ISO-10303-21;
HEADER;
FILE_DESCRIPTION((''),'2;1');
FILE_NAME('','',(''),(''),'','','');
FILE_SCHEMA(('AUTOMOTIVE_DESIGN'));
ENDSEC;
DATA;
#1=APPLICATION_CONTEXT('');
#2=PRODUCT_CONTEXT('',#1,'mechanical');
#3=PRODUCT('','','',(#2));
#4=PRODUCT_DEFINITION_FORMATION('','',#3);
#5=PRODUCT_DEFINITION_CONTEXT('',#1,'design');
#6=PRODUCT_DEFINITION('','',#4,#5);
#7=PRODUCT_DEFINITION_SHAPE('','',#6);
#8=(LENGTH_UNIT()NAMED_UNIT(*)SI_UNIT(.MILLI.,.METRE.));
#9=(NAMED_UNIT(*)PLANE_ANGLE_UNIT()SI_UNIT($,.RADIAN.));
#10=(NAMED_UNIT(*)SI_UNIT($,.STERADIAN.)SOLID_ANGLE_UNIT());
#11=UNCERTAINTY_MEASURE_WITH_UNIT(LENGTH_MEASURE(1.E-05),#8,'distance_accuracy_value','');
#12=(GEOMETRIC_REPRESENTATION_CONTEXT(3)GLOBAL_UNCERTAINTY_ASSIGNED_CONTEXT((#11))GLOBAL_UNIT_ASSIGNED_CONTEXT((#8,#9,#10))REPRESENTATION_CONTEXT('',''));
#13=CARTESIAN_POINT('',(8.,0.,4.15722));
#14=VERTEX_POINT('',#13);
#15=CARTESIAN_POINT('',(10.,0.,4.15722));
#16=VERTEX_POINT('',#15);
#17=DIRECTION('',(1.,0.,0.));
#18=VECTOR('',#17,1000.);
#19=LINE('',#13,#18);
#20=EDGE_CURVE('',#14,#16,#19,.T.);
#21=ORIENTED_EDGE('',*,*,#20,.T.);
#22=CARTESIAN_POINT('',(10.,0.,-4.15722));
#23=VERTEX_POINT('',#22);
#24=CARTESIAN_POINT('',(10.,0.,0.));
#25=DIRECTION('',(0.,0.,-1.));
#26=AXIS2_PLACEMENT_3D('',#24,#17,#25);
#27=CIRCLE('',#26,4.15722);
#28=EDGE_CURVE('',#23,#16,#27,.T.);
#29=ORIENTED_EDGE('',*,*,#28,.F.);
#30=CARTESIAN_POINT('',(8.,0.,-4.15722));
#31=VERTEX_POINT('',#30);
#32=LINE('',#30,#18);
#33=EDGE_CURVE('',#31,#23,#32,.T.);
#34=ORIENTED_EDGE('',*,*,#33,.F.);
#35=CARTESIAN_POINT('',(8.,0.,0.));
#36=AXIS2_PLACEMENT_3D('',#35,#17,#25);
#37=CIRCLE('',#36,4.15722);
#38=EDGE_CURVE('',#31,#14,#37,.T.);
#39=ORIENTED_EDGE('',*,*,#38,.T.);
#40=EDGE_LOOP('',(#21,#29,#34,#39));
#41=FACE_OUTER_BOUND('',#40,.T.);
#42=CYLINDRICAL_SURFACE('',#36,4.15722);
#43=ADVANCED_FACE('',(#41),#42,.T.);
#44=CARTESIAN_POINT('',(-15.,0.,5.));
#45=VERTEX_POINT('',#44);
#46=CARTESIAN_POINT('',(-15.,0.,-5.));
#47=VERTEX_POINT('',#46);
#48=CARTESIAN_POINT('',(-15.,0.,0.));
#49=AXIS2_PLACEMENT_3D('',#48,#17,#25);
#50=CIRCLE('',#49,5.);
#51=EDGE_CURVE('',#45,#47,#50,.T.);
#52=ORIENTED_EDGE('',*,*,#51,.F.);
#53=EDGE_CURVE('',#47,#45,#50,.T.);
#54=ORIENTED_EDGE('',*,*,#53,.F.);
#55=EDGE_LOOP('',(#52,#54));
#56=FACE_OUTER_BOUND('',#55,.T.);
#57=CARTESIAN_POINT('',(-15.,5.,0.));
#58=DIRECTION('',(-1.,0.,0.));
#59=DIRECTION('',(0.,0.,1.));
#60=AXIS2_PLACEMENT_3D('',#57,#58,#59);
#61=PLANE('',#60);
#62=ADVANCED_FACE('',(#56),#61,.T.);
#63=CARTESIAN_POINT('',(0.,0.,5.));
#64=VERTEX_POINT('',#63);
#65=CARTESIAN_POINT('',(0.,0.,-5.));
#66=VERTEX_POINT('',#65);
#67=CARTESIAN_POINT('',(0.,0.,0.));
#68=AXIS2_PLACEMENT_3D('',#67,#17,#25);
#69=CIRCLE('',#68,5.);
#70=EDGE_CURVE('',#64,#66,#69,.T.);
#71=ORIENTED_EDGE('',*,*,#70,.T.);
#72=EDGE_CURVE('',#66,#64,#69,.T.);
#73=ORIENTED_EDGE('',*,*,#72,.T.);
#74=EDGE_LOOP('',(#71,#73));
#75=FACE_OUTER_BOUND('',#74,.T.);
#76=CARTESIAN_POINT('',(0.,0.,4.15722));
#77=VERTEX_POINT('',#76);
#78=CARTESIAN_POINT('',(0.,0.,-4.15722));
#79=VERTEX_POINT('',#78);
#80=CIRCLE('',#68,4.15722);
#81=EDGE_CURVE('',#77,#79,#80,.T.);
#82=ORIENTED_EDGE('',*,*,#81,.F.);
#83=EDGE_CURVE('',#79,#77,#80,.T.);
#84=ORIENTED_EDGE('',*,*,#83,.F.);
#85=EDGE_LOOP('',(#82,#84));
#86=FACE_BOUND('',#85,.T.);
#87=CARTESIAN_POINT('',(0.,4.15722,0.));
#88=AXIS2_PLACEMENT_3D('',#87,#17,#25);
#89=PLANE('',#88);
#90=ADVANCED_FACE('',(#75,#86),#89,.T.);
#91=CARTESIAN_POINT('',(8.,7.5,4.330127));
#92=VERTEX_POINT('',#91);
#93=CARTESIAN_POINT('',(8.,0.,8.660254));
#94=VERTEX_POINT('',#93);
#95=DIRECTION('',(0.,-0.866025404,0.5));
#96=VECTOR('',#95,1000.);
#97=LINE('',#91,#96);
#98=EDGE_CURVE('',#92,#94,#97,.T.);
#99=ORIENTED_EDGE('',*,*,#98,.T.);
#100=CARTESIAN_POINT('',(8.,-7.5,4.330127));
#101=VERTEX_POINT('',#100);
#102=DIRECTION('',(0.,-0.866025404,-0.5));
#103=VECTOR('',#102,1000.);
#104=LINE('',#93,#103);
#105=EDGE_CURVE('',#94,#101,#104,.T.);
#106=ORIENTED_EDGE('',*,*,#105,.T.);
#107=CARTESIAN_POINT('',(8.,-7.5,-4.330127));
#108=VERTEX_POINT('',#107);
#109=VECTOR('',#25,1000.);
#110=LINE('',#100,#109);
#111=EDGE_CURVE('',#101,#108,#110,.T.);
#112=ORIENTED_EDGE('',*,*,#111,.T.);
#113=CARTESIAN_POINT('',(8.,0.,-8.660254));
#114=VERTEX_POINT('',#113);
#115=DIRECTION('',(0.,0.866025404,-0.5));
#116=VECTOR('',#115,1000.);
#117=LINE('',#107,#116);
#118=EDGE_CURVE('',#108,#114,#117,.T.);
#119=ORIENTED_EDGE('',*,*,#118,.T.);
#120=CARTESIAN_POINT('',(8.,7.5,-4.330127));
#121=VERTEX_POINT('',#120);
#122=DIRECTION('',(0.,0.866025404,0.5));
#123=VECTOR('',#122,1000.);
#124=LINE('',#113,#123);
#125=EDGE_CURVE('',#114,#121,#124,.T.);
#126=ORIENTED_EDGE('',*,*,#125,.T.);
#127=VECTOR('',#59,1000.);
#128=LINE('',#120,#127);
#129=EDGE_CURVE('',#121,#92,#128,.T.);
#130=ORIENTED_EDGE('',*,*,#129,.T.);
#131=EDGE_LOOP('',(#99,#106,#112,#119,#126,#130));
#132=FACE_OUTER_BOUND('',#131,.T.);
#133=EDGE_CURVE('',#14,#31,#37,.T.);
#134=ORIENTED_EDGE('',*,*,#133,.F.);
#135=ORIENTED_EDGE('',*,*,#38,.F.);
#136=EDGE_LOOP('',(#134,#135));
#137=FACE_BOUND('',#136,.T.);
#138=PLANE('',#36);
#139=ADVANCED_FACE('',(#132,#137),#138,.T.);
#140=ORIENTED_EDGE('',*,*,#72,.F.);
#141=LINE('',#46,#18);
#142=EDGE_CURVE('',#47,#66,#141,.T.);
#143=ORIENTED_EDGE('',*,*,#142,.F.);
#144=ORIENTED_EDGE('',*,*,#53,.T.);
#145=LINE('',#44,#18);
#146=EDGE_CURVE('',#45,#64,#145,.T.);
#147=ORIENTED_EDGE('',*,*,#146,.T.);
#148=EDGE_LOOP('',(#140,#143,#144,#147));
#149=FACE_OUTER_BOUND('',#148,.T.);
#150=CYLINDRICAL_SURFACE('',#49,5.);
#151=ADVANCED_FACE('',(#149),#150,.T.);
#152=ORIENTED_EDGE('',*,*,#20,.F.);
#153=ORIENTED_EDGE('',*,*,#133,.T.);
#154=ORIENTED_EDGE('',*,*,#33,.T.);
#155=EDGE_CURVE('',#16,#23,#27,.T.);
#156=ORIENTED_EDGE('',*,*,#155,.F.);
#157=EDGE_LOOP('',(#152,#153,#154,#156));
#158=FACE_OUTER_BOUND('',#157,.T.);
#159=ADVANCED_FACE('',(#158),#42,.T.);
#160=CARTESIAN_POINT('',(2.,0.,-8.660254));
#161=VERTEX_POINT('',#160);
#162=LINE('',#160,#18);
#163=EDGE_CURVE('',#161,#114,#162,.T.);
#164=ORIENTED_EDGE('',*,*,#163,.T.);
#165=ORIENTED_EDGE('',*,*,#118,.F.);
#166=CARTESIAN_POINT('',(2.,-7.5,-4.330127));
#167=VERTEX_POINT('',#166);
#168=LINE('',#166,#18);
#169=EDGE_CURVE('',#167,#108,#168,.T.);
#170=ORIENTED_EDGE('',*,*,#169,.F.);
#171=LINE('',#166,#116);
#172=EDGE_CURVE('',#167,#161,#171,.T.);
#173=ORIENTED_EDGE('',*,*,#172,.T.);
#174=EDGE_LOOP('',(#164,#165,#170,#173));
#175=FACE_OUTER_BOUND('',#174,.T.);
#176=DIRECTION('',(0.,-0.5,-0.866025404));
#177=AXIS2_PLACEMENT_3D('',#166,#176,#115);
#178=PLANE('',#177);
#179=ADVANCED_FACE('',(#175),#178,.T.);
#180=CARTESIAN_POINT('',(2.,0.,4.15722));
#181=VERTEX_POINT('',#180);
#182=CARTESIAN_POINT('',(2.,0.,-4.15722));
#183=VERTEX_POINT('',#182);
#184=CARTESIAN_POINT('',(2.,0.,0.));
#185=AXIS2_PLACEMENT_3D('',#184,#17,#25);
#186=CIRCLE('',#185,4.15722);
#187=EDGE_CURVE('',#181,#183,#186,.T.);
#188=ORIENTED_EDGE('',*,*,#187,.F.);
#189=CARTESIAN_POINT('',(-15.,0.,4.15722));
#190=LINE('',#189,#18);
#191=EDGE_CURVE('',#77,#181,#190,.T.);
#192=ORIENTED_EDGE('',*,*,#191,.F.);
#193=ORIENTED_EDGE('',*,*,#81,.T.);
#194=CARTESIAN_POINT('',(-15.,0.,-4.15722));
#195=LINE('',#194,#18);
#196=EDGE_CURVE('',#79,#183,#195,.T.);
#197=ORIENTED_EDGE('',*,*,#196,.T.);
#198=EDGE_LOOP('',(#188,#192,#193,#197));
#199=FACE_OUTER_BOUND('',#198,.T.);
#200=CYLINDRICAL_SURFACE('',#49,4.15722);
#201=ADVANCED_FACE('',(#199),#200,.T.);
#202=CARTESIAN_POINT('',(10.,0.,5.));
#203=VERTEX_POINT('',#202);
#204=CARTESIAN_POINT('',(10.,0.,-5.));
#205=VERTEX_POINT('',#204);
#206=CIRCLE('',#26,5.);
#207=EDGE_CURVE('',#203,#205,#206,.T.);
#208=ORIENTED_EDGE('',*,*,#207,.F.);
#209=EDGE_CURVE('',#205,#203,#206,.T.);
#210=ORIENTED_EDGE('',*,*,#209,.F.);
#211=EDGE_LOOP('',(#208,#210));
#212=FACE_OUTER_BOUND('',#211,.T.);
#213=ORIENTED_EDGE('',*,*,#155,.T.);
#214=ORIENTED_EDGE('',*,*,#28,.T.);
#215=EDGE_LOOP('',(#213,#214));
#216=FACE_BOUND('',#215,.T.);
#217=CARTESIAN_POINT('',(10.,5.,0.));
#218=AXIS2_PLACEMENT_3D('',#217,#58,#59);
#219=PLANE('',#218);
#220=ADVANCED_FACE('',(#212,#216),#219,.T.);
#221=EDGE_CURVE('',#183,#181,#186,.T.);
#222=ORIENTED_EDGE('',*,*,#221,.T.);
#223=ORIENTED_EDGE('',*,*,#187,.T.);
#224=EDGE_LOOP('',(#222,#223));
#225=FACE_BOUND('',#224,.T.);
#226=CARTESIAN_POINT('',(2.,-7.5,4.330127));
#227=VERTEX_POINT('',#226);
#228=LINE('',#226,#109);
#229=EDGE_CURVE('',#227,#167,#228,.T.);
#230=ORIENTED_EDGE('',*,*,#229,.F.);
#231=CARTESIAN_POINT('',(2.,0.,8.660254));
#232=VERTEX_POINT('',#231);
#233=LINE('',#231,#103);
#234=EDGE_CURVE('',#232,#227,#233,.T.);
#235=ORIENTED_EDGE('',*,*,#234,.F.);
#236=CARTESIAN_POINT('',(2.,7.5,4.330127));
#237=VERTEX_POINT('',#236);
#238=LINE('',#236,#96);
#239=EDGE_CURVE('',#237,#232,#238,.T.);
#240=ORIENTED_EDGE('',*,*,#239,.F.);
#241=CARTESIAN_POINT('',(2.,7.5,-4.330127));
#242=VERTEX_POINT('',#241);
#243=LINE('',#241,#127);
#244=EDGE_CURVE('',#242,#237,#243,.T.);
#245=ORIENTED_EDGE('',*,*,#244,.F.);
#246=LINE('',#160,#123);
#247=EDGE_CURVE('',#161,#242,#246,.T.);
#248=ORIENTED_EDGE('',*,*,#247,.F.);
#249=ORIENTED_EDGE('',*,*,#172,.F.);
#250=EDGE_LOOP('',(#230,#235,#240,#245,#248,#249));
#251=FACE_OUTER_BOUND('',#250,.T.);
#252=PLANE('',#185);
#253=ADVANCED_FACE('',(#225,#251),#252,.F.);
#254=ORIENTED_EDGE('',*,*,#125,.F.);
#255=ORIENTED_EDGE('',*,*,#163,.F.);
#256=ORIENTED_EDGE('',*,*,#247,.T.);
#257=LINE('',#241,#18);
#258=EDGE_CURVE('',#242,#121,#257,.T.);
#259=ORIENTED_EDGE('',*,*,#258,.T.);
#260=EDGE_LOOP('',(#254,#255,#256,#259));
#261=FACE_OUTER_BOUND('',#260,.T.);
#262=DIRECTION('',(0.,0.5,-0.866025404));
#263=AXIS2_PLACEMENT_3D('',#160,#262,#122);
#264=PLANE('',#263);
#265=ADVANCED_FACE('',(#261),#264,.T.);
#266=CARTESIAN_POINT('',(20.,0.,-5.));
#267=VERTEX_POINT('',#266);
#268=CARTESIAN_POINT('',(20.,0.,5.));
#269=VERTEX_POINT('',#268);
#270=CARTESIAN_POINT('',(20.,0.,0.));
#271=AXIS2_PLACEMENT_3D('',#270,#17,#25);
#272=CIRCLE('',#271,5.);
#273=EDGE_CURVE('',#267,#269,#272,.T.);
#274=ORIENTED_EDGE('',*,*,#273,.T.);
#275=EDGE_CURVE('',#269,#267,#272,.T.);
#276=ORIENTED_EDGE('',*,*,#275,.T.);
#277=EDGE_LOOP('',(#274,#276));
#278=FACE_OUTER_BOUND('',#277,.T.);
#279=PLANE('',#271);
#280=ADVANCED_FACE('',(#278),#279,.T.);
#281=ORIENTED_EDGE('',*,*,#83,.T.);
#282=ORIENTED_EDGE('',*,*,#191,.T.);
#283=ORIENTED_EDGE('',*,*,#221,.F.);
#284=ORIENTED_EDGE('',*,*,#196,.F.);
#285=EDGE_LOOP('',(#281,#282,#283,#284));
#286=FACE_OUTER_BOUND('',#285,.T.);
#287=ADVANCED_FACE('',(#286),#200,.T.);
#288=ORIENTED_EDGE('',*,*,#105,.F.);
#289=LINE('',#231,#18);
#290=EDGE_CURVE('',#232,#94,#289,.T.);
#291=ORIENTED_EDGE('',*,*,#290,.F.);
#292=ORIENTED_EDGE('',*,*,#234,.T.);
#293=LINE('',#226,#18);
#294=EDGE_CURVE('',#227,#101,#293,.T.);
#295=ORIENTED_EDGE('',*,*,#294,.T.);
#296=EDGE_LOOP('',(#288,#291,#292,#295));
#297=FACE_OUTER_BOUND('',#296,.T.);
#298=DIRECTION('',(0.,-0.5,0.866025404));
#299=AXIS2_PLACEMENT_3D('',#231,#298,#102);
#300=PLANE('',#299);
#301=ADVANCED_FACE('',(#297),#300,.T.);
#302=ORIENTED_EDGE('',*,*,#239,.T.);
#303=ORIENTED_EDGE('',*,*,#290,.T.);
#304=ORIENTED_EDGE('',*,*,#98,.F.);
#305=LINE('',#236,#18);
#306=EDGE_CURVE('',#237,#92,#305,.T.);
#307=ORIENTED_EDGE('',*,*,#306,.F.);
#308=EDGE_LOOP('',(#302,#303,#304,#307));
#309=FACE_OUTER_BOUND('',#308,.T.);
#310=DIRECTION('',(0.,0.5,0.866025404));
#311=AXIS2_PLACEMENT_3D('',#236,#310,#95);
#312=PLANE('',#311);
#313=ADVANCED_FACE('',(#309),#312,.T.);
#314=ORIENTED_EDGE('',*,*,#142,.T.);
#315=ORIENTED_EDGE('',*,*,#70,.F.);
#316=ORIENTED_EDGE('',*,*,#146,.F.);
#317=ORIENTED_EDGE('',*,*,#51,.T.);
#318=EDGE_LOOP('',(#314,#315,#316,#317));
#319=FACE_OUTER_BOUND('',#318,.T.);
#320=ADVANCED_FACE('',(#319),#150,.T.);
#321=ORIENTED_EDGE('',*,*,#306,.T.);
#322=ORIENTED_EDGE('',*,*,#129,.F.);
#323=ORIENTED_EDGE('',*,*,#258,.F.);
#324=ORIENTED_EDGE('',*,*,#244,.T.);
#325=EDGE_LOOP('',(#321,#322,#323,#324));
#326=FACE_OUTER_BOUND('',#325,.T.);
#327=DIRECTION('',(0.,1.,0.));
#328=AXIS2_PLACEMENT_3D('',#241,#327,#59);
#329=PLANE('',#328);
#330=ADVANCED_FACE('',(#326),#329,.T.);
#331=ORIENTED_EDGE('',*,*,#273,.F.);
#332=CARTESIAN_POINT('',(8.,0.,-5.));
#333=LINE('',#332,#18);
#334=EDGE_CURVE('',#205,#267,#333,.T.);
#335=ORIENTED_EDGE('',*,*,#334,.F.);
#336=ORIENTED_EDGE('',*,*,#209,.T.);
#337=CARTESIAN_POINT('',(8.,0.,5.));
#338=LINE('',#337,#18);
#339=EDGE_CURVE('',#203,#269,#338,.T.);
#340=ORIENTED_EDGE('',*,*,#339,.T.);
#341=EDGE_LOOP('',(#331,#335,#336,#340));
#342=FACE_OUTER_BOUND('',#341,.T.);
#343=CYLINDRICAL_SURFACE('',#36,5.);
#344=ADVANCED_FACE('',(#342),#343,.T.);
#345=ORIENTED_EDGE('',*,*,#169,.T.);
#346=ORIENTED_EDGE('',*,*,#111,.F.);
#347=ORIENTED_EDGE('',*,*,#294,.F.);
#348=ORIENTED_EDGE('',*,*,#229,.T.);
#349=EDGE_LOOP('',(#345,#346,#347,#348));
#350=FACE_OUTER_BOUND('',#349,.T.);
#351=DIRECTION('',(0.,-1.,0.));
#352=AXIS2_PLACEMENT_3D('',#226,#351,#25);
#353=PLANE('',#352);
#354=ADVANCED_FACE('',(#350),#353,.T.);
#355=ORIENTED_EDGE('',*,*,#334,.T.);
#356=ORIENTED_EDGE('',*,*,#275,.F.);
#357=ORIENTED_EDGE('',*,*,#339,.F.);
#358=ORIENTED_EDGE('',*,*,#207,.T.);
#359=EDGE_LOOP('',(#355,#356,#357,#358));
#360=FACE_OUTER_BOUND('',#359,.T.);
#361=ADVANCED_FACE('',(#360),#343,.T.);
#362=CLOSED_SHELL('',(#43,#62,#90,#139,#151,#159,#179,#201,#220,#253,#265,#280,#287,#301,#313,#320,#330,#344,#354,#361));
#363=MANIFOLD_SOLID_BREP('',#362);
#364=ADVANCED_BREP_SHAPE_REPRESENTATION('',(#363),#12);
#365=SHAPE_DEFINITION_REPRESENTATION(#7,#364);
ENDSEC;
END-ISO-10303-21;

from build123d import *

# Parameters (mm, degrees)
EXTRUDE_1_DEPTH = 6


with BuildPart() as part:
    # 草图1 → 凸台-拉伸1 (new body)
    with BuildSketch(Plane(origin=(8, 0, 0), x_dir=(0, 0, -1), z_dir=(1, 0, 0))):
        Polygon((-8.660254038, 0), (-4.330127019, -7.5), (4.330127019, -7.5), (8.660254038, 0), (4.330127019, 7.5), (-4.330127019, 7.5), align=None)
    extrude(amount=-EXTRUDE_1_DEPTH)

    # 草图2 → 旋转1 (revolve)
    with BuildSketch(Plane.XY, mode=Mode.PRIVATE) as revolve_1_sk:
        Polygon((-15, 5), (-15, 0), (2, 0), (2, 4.157220044), (0, 4.157220044), (0, 5), align=None)
    revolve(revolve_1_sk.sketch.rotate(Axis((-15, 0, 0), (1, 0, 0)), 270), axis=Axis((-15, 0, 0), (1, 0, 0)))

    # 草图3 → 旋转2 (revolve)
    with BuildSketch(Plane.XY, mode=Mode.PRIVATE) as revolve_2_sk:
        Polygon((8, 4.157220044), (8, 0), (20, 0), (20, 5), (10, 5), (10, 4.157220044), align=None)
    revolve(revolve_2_sk.sketch.rotate(Axis((8, 0, 0), (1, 0, 0)), 270), axis=Axis((8, 0, 0), (1, 0, 0)))


solid = part.part
